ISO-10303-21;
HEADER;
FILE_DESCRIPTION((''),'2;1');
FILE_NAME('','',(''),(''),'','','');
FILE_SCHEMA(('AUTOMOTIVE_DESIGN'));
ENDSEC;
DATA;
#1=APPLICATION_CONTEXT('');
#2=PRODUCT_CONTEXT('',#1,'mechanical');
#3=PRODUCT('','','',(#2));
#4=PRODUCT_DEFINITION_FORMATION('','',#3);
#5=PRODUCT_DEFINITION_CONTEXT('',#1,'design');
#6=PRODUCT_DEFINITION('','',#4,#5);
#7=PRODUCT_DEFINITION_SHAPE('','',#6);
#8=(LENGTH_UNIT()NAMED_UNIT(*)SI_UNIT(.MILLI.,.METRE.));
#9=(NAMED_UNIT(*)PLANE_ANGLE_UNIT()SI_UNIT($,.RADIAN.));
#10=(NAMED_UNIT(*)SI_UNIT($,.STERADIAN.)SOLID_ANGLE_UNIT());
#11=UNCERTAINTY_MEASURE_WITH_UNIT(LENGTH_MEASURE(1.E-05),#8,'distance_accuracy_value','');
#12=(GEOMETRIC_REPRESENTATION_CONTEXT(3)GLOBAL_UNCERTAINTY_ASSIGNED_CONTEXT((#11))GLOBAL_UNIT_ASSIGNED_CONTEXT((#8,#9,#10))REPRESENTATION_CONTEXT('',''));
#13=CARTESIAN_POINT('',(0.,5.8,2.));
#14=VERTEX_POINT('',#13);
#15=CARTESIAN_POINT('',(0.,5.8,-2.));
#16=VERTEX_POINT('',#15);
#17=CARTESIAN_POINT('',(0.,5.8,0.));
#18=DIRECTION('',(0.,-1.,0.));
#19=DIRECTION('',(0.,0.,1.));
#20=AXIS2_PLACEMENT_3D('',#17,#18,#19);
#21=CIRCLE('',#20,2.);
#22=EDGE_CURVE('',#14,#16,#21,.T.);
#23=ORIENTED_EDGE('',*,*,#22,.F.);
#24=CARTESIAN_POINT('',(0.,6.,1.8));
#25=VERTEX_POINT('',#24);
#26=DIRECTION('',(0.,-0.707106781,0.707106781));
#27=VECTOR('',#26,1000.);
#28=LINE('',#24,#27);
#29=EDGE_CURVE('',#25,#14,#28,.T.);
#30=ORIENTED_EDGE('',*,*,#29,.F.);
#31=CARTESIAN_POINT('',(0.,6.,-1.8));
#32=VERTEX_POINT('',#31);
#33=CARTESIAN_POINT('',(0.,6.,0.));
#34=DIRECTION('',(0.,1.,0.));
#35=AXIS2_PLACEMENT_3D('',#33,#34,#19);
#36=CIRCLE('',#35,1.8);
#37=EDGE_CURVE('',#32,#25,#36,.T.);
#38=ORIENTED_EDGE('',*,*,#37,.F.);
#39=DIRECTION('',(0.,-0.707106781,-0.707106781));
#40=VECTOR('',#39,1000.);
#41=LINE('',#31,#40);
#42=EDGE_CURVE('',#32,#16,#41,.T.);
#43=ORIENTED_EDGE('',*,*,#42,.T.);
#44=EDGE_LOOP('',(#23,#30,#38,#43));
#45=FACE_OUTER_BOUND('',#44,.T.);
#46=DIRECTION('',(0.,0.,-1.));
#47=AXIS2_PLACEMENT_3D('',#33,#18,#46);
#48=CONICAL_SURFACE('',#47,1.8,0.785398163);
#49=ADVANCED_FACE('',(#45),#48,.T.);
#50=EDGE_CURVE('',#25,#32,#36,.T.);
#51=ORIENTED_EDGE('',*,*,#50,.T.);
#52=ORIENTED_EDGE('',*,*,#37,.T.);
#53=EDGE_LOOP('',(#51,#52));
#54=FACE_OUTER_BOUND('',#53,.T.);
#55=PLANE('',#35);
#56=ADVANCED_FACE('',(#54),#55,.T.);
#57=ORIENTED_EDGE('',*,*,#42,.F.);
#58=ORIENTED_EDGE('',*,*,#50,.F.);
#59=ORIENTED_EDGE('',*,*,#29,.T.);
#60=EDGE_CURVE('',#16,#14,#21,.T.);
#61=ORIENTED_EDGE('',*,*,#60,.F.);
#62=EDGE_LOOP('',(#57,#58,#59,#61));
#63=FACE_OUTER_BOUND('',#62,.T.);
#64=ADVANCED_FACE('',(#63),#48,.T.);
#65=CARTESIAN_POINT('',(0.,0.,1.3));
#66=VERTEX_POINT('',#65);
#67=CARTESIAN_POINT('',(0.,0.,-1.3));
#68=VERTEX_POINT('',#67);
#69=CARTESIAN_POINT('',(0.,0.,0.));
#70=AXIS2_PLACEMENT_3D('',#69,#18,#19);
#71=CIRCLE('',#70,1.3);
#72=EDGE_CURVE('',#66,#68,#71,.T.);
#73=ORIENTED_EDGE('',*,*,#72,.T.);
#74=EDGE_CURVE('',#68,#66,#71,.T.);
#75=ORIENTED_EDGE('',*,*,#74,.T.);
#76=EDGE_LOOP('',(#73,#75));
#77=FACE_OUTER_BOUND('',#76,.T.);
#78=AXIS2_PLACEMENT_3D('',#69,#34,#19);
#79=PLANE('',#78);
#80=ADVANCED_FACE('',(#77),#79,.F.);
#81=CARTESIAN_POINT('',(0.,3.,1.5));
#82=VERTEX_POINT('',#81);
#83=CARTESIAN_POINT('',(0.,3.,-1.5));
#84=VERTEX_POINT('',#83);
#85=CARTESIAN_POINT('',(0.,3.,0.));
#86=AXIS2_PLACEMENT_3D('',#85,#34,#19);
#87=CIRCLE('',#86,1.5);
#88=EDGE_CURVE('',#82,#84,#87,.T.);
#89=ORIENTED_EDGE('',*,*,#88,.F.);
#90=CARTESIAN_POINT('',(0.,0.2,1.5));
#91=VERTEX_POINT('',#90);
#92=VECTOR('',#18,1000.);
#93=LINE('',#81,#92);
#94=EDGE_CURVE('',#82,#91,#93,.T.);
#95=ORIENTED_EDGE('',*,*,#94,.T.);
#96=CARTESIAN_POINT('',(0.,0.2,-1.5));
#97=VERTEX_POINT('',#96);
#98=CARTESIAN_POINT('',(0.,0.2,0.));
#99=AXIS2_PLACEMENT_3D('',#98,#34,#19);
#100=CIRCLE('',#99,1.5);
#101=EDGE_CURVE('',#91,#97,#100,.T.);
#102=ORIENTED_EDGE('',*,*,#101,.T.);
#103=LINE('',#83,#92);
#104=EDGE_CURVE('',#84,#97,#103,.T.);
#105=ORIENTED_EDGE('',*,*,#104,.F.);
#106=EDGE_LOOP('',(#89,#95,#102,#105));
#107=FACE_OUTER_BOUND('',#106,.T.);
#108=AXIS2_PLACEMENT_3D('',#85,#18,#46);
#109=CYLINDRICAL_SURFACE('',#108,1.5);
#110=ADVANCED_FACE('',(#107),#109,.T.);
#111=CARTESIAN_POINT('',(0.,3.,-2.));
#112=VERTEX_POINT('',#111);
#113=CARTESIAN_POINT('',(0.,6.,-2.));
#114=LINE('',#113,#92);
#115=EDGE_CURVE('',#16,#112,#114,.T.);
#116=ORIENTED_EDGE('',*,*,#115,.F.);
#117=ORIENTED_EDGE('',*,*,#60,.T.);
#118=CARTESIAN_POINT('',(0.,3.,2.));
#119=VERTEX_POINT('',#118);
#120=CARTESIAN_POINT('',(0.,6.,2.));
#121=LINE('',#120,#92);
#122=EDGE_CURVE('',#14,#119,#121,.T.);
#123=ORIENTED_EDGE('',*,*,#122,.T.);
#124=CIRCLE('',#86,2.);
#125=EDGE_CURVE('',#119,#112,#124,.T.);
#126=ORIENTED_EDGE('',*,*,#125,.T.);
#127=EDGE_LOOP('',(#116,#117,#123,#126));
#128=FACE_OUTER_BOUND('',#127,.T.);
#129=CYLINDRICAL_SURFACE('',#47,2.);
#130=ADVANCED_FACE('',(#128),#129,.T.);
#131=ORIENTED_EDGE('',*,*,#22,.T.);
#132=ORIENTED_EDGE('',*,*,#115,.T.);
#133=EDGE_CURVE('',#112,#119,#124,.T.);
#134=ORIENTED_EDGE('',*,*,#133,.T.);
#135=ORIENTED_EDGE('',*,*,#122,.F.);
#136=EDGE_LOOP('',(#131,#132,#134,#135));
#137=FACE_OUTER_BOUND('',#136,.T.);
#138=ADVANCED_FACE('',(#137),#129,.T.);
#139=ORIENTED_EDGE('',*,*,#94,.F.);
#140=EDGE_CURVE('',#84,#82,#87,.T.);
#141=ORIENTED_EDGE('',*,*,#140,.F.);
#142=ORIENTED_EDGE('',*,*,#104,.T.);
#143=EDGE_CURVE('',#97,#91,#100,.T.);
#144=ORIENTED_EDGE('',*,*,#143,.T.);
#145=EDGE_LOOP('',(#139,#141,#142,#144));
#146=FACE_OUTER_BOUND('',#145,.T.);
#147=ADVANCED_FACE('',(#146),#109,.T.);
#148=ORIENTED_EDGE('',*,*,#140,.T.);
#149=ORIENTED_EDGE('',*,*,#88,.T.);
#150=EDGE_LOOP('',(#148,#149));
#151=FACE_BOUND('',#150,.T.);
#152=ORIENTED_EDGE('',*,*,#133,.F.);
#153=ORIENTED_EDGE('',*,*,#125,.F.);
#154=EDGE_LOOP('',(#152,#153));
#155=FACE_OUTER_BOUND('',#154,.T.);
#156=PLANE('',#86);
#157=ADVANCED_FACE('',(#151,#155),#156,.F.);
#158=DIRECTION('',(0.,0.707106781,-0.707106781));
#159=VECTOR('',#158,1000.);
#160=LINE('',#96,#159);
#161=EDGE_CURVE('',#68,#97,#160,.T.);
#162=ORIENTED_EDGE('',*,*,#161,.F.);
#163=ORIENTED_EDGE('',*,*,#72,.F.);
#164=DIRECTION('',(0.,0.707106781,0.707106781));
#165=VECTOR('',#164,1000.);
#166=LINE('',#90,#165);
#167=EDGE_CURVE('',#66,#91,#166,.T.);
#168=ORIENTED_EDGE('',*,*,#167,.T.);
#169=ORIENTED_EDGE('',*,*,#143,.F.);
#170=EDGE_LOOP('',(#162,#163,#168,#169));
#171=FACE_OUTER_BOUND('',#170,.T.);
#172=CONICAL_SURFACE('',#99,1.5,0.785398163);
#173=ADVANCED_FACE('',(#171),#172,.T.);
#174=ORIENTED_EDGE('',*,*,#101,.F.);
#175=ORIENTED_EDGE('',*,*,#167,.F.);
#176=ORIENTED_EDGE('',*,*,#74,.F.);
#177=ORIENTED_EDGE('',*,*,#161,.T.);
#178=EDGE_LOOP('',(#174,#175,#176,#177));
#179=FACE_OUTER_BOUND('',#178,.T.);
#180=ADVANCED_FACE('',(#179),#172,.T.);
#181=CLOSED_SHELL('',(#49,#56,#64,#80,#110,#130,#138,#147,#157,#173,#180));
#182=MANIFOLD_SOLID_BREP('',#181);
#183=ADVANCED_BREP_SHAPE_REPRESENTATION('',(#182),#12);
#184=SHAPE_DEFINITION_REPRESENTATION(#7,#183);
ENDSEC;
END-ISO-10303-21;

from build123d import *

# Parameters (mm, degrees)
SKETCH1_R           = 1.5
BOSS_EXTRUDE1_DEPTH = 3
SKETCH2_R           = 2
BOSS_EXTRUDE2_DEPTH = 3
CHAMFER1_SIZE       = 0.2


with BuildPart() as part:
    # Sketch1 → Boss-Extrude1 (new body)
    with BuildSketch(Plane(origin=(0, 0, 0), x_dir=(1, 0, 0), z_dir=(0, 1, 0))):
        with Locations(Location((0, 0, 0), (0, 0, 270))):
            Circle(SKETCH1_R)
    extrude(amount=BOSS_EXTRUDE1_DEPTH)

    # Sketch2 → Boss-Extrude2 (add)
    with BuildSketch(Plane(origin=(0, 3, 0), x_dir=(1, 0, 0), z_dir=(0, 1, 0))):
        with Locations(Location((0, 0, 0), (0, 0, 270))):
            Circle(SKETCH2_R)
    extrude(amount=BOSS_EXTRUDE2_DEPTH)

    # Chamfer1
    chamfer1_edges = [part.edges().sort_by_distance(p)[0] for p in [
        (0, 0, -1.5),
        (0, 6, -2),
    ]]
    chamfer(chamfer1_edges, length=CHAMFER1_SIZE)


solid = part.part
